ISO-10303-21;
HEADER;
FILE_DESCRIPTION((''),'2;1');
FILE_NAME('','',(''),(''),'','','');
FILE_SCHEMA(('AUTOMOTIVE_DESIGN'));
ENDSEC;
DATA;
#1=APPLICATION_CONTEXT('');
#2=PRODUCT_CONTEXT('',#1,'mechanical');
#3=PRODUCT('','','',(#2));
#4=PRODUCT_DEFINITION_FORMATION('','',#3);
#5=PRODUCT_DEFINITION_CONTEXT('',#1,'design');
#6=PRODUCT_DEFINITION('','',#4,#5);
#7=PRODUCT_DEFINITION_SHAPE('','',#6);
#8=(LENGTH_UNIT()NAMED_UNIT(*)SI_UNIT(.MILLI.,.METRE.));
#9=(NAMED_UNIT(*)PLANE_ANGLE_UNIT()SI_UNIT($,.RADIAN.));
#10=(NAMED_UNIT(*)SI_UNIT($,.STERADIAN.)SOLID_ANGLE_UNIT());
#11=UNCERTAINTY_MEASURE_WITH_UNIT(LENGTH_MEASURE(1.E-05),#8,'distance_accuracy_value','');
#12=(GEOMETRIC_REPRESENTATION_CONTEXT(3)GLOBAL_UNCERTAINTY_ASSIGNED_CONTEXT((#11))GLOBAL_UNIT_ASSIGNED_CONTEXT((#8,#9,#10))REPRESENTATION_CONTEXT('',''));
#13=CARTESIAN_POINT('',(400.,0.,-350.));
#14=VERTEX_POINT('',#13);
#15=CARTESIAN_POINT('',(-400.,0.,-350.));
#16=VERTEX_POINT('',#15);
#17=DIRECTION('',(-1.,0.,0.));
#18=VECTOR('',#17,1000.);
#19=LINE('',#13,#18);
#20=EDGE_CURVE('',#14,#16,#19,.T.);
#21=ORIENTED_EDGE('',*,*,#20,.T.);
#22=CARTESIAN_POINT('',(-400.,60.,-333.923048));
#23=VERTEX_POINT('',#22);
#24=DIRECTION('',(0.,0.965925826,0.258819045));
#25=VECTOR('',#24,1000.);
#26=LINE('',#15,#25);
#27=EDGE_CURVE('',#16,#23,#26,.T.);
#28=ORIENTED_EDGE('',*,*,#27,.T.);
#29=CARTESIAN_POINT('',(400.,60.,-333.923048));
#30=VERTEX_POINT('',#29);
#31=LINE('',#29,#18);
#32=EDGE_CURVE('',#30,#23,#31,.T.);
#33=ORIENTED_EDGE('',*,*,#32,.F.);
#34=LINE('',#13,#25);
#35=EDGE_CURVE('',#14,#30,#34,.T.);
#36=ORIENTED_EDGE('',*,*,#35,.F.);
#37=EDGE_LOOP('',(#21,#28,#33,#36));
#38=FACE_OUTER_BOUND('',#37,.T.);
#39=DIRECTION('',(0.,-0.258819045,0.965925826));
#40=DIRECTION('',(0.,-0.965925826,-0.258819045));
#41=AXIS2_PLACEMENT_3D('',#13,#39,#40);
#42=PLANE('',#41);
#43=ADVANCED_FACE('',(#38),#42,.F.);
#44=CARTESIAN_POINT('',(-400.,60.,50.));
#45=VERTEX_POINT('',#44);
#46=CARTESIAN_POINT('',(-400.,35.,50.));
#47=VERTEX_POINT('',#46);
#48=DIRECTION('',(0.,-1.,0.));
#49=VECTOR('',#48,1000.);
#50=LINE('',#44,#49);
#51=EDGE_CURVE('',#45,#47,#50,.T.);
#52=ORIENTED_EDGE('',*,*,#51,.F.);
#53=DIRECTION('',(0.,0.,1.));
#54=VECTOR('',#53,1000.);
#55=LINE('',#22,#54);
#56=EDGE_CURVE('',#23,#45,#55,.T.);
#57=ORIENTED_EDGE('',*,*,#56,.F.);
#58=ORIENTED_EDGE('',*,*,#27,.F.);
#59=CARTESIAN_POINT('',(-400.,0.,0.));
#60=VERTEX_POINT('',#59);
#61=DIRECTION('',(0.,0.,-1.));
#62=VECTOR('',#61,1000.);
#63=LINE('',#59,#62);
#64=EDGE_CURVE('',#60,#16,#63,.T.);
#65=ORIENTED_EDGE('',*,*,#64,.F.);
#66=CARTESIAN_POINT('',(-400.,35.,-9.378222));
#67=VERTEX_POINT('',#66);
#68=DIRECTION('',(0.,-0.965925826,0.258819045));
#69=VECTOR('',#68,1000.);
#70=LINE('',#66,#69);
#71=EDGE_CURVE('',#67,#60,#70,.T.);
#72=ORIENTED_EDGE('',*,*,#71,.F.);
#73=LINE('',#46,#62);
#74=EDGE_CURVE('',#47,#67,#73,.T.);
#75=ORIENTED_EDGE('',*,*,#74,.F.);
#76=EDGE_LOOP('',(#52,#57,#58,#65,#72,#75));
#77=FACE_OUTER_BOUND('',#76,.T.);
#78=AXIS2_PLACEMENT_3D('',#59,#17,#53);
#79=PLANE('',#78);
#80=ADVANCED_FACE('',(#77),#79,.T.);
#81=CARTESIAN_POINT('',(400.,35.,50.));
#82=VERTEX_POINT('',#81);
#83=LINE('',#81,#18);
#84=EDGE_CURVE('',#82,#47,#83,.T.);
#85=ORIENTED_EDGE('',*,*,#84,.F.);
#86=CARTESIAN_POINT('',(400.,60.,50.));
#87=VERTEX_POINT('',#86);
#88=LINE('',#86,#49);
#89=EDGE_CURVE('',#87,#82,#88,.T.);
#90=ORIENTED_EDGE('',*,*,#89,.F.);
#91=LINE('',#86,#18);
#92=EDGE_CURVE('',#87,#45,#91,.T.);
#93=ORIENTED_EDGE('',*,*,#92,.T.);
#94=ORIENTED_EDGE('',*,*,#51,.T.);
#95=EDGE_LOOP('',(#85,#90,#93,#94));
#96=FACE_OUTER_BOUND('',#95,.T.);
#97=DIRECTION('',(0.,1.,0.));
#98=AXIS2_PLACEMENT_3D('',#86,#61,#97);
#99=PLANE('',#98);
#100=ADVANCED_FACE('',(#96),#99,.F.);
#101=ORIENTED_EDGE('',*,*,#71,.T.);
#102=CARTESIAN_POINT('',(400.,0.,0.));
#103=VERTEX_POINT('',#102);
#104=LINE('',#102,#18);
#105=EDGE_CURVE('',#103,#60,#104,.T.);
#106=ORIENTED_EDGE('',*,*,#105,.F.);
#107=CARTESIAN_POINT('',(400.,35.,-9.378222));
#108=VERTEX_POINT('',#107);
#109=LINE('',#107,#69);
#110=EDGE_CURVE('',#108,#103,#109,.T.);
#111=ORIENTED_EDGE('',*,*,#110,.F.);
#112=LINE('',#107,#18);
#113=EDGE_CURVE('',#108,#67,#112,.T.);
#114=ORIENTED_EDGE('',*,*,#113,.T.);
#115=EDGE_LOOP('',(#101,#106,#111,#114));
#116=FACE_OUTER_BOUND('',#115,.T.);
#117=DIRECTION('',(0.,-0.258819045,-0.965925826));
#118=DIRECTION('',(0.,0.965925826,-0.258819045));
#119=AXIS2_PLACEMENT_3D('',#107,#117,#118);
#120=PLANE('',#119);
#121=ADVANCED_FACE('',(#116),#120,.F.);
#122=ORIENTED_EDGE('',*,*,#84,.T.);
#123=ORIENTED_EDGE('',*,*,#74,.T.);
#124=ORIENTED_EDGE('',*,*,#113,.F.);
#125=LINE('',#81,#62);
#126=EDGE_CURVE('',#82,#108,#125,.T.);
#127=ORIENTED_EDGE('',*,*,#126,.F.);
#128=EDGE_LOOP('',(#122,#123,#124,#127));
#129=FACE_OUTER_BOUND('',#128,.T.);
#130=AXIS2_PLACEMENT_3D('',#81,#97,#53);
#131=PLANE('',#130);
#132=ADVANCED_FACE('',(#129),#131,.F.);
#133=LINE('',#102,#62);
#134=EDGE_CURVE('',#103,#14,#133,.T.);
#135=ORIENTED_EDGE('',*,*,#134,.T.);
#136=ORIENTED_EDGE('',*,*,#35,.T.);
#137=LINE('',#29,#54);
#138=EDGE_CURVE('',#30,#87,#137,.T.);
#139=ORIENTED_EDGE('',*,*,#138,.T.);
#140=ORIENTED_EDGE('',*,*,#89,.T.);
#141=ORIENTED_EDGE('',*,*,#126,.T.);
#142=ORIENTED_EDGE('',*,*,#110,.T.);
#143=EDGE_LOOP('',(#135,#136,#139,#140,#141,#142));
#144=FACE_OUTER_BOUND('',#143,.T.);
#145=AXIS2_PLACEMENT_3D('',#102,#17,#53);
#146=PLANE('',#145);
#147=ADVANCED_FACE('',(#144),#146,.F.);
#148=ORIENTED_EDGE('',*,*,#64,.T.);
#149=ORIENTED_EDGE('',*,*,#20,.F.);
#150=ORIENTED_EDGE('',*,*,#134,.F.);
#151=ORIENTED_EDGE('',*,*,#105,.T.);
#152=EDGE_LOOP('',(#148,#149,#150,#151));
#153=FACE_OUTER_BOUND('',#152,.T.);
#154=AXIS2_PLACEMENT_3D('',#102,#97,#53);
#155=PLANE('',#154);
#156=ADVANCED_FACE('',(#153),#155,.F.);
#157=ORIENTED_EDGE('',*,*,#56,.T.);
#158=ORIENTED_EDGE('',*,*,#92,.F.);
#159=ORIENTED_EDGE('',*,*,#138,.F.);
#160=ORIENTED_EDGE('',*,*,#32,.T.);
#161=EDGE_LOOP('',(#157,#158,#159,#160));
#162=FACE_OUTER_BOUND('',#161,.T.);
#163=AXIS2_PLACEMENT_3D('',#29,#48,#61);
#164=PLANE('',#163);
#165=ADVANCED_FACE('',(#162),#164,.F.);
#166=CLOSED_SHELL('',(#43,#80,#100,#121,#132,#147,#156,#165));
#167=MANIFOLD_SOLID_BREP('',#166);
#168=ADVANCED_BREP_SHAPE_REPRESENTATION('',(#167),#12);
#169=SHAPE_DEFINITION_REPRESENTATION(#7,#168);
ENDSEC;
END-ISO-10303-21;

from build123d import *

# Parameters (mm, degrees)
BOSS_EXTRUDE1_DEPTH = 400


with BuildPart() as part:
    # Sketch1 → Boss-Extrude1 (new, symmetric)
    with BuildSketch(Plane(origin=(0, 0, 0), x_dir=(0, 0, -1), z_dir=(1, 0, 0))):
        Polygon((350, 0), (333.923048454, 60), (-50, 60), (-50, 35), (9.378221735, 35), (0, 0), align=None)
    extrude(amount=BOSS_EXTRUDE1_DEPTH, both=True)


solid = part.part
